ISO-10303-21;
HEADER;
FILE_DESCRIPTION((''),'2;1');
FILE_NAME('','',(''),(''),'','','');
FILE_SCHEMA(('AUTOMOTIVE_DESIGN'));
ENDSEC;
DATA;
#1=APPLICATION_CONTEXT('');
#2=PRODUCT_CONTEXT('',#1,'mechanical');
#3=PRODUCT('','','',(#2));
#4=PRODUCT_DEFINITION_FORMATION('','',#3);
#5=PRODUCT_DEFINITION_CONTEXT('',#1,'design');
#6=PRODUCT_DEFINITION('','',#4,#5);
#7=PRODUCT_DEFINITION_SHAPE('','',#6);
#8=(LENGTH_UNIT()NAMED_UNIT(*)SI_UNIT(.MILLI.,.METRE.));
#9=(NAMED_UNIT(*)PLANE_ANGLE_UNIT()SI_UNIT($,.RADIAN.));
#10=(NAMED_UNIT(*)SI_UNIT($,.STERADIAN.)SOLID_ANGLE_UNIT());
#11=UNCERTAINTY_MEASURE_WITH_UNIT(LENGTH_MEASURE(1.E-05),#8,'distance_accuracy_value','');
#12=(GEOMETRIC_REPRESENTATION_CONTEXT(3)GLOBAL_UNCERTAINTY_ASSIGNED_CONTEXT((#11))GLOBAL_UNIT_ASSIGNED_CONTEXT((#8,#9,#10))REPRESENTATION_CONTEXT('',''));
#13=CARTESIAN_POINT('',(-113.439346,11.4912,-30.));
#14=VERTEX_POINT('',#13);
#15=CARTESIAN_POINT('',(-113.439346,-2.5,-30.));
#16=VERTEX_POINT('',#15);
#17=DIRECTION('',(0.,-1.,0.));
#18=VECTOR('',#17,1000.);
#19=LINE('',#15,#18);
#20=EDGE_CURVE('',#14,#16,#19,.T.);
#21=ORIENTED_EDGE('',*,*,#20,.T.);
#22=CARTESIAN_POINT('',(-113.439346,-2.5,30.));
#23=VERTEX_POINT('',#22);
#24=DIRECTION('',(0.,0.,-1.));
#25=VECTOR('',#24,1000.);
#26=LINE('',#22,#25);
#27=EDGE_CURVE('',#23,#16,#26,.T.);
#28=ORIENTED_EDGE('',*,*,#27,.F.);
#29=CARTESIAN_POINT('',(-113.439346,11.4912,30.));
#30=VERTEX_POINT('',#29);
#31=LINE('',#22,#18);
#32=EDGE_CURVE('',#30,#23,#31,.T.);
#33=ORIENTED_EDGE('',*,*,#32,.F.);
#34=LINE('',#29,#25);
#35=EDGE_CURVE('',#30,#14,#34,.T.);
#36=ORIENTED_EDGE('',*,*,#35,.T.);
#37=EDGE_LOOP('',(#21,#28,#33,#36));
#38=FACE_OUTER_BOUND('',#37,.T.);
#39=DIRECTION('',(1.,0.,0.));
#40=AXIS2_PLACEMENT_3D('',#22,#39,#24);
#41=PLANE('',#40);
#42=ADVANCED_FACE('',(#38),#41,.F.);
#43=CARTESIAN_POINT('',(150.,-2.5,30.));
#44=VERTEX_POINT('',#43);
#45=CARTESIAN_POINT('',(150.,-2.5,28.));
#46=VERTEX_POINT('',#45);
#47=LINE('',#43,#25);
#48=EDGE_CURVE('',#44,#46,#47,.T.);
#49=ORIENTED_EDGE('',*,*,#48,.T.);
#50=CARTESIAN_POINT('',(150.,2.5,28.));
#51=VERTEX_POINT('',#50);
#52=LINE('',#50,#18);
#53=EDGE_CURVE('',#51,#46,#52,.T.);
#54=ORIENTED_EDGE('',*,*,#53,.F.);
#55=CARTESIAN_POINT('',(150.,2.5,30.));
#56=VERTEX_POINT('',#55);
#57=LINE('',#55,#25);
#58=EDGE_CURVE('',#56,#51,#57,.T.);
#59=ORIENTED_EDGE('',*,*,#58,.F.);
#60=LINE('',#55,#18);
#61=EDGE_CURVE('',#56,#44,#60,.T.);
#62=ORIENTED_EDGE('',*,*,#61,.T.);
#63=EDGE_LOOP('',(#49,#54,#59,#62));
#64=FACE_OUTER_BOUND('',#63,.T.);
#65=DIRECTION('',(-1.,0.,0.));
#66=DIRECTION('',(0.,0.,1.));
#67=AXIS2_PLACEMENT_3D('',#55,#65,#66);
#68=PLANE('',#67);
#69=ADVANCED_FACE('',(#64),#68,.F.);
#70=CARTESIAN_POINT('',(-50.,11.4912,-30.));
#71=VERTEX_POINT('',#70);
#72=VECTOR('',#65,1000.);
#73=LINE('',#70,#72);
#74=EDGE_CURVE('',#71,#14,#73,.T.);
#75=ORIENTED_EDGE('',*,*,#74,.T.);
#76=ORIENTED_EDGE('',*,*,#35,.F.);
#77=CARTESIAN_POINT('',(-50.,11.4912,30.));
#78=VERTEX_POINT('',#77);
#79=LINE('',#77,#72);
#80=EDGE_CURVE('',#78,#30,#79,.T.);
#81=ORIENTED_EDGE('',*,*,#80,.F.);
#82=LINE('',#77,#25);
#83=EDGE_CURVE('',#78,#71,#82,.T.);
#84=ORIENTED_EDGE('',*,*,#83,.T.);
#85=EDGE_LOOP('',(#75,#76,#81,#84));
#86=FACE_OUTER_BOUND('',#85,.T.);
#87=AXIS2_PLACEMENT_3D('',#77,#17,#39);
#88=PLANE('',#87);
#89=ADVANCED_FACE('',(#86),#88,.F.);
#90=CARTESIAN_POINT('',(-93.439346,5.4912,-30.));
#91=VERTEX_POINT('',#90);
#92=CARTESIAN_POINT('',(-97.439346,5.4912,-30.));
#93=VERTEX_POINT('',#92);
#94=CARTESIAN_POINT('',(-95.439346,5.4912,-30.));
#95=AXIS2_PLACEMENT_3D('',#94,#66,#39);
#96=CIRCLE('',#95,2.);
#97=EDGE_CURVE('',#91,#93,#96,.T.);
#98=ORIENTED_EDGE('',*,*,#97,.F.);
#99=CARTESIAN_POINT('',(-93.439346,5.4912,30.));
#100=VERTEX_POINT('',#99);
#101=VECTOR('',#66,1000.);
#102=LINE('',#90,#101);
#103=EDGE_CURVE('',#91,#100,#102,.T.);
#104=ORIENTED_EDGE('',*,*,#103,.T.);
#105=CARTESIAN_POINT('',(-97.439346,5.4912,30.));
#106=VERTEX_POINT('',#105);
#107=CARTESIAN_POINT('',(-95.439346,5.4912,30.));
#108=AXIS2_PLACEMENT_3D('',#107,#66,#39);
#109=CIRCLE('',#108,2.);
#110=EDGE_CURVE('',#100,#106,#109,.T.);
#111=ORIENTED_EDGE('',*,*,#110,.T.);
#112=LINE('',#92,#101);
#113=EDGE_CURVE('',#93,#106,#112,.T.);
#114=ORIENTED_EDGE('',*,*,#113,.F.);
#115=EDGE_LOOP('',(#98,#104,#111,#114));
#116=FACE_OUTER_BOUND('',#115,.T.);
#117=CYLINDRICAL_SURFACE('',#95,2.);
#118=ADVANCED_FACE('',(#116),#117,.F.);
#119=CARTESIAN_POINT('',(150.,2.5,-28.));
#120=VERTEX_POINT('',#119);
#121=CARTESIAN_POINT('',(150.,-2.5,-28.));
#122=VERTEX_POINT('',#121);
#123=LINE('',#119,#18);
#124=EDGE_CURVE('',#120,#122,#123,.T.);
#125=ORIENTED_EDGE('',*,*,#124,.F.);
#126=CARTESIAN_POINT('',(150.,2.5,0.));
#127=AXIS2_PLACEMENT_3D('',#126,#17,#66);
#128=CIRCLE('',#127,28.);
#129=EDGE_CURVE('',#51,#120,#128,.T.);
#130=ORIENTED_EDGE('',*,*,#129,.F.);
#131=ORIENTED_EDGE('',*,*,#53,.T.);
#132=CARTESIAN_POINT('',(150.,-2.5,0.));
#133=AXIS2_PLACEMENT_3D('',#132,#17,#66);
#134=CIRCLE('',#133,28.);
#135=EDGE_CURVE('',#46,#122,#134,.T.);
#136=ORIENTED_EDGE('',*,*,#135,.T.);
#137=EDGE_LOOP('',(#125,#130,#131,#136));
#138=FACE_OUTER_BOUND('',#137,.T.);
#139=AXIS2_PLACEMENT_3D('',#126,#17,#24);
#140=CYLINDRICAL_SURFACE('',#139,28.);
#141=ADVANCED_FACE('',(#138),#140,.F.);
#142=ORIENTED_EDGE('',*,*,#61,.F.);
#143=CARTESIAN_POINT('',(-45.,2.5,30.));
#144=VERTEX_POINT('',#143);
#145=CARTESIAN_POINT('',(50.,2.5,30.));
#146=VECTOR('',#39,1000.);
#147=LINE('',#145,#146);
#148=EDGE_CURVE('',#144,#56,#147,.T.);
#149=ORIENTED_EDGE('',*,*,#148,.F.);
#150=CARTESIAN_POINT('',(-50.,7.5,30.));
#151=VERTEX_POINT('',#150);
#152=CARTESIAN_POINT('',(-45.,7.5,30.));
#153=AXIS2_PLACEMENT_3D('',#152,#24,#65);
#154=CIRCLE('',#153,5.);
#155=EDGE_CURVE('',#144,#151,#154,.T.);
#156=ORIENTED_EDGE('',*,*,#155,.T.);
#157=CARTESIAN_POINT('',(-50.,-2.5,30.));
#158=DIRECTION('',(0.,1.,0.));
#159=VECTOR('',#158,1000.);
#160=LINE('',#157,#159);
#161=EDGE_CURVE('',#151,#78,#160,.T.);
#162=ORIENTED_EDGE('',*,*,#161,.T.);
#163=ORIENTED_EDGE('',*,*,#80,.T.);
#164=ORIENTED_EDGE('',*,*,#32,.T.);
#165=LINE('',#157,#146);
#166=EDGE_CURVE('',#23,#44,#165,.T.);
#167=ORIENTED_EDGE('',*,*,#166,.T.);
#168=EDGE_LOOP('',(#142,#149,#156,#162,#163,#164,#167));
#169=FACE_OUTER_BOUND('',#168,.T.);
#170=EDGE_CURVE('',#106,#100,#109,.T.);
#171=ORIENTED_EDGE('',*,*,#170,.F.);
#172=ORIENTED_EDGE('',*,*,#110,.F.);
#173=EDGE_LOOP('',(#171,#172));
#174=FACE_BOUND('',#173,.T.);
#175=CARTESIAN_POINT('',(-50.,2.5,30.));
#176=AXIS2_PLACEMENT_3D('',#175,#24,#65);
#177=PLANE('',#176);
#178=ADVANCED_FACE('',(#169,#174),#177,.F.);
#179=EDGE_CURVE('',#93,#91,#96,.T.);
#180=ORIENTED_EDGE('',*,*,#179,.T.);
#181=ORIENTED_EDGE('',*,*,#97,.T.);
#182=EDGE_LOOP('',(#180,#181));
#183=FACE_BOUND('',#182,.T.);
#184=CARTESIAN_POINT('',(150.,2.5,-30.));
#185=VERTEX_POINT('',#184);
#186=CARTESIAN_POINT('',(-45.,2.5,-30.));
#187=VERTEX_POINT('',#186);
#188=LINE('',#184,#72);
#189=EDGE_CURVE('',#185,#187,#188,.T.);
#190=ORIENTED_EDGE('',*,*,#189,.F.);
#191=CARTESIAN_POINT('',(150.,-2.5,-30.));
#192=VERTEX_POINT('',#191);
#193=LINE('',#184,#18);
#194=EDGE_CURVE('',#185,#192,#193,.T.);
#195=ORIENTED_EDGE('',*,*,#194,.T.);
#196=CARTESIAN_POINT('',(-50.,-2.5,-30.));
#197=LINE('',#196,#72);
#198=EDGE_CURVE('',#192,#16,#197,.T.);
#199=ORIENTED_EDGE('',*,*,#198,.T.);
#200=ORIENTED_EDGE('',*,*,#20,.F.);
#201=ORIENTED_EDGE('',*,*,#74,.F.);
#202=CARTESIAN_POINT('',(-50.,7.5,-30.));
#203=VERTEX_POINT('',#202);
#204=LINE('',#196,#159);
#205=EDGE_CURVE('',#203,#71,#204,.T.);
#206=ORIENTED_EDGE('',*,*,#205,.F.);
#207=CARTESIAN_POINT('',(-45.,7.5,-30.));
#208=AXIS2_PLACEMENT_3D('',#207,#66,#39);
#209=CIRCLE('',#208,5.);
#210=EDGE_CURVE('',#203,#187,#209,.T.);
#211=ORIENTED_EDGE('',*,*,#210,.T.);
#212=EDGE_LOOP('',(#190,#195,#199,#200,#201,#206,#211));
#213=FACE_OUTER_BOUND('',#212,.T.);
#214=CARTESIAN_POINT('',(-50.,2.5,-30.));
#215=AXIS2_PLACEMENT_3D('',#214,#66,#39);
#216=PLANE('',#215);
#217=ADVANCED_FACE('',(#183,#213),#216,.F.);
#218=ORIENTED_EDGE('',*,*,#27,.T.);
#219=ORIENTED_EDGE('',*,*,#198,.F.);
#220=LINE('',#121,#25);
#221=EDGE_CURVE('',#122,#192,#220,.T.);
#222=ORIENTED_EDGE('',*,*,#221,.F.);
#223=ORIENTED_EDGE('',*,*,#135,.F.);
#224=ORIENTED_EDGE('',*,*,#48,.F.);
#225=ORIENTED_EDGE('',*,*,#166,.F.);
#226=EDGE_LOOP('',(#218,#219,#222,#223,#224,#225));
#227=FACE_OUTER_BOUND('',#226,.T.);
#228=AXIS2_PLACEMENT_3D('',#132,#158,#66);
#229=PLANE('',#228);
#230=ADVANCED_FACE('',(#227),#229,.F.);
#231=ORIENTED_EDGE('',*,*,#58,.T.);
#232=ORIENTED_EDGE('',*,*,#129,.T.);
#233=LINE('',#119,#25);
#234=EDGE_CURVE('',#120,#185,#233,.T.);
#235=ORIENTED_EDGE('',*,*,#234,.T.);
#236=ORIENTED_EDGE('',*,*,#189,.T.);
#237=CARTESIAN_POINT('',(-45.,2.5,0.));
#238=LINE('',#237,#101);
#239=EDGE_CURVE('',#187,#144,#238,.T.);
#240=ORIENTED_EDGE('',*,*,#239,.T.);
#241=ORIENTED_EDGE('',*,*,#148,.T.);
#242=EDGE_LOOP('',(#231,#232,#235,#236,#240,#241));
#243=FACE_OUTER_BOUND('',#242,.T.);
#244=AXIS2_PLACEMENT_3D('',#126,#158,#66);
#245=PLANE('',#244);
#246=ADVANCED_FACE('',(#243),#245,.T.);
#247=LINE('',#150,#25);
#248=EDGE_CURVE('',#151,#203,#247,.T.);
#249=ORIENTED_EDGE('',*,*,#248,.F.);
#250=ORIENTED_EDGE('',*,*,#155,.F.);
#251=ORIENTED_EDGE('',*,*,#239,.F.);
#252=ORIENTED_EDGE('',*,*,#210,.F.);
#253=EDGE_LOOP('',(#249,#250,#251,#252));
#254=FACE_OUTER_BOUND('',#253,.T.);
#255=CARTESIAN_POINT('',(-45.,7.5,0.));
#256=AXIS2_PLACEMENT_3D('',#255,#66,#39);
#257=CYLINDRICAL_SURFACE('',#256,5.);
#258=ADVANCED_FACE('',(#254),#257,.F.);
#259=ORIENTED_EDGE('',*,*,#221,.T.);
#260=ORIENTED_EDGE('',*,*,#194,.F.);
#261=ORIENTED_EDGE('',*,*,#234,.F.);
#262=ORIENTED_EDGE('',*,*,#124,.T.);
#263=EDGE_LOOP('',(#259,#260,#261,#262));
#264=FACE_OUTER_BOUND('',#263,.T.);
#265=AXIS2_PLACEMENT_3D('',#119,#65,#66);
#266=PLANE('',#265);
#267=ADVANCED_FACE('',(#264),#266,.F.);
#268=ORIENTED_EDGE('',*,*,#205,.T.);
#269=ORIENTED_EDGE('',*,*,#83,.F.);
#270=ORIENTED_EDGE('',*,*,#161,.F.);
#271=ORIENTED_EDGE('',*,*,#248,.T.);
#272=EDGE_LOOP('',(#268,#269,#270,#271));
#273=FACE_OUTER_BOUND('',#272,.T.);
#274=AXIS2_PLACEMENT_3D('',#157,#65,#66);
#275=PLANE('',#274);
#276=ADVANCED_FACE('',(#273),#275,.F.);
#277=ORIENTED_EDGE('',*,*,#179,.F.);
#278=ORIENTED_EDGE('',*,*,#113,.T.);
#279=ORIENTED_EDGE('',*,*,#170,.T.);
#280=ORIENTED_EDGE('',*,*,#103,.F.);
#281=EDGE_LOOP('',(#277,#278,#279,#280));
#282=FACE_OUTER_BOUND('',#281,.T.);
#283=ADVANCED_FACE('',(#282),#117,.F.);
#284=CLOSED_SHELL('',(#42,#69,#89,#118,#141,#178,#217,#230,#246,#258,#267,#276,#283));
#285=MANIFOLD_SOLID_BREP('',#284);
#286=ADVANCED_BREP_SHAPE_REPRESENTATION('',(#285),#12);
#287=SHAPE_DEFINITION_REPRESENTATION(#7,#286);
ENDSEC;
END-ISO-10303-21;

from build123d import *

# Parameters (mm, degrees)
BOSS_EXTRUDE2_DEPTH = 2.5
SKETCH5_W           = 63.43934648
SKETCH5_H           = 13.991199956
BOSS_EXTRUDE3_DEPTH = 30
FILLET1_R           = 5
SKETCH6_R           = 2
CUT_EXTRUDE1_DEPTH  = 162.963105911


with BuildPart() as part:
    # Sketch2 → Boss-Extrude2 (new, symmetric)
    with BuildSketch(Plane(origin=(0, 0, 0), x_dir=(1, 0, 0), z_dir=(0, 1, 0))):
        with BuildLine():
            Line((-50, 30), (50, 30))
            Line((50, 30), (150, 30))
            Line((150, 30), (150, 28))
            ThreePointArc((150, 28), (122, 0), (150, -28))
            Line((150, -28), (150, -30))
            Line((150, -30), (50, -30))
            Line((50, -30), (-50, -30))
            Line((-50, -30), (-50, 30))
        make_face()
    extrude(amount=BOSS_EXTRUDE2_DEPTH, both=True)

    # Sketch5 → Boss-Extrude3 (add, symmetric)
    with BuildSketch(Plane.XY):
        with Locations((-81.71967324, 4.495599978)):
            Rectangle(SKETCH5_W, SKETCH5_H)
    extrude(amount=BOSS_EXTRUDE3_DEPTH, both=True)

    # Fillet1
    fillet1_edges = [part.edges().sort_by_distance(p)[0] for p in [
        (-50, 2.5, 0),
    ]]
    fillet(fillet1_edges, radius=FILLET1_R)

    # Sketch6 → Cut-Extrude1 (cut, through all)
    with BuildSketch(Plane.XY.offset(30)):
        with Locations((-95.43934648, 5.491199956)):
            Circle(SKETCH6_R)
    extrude(amount=-CUT_EXTRUDE1_DEPTH, mode=Mode.SUBTRACT)


solid = part.part
